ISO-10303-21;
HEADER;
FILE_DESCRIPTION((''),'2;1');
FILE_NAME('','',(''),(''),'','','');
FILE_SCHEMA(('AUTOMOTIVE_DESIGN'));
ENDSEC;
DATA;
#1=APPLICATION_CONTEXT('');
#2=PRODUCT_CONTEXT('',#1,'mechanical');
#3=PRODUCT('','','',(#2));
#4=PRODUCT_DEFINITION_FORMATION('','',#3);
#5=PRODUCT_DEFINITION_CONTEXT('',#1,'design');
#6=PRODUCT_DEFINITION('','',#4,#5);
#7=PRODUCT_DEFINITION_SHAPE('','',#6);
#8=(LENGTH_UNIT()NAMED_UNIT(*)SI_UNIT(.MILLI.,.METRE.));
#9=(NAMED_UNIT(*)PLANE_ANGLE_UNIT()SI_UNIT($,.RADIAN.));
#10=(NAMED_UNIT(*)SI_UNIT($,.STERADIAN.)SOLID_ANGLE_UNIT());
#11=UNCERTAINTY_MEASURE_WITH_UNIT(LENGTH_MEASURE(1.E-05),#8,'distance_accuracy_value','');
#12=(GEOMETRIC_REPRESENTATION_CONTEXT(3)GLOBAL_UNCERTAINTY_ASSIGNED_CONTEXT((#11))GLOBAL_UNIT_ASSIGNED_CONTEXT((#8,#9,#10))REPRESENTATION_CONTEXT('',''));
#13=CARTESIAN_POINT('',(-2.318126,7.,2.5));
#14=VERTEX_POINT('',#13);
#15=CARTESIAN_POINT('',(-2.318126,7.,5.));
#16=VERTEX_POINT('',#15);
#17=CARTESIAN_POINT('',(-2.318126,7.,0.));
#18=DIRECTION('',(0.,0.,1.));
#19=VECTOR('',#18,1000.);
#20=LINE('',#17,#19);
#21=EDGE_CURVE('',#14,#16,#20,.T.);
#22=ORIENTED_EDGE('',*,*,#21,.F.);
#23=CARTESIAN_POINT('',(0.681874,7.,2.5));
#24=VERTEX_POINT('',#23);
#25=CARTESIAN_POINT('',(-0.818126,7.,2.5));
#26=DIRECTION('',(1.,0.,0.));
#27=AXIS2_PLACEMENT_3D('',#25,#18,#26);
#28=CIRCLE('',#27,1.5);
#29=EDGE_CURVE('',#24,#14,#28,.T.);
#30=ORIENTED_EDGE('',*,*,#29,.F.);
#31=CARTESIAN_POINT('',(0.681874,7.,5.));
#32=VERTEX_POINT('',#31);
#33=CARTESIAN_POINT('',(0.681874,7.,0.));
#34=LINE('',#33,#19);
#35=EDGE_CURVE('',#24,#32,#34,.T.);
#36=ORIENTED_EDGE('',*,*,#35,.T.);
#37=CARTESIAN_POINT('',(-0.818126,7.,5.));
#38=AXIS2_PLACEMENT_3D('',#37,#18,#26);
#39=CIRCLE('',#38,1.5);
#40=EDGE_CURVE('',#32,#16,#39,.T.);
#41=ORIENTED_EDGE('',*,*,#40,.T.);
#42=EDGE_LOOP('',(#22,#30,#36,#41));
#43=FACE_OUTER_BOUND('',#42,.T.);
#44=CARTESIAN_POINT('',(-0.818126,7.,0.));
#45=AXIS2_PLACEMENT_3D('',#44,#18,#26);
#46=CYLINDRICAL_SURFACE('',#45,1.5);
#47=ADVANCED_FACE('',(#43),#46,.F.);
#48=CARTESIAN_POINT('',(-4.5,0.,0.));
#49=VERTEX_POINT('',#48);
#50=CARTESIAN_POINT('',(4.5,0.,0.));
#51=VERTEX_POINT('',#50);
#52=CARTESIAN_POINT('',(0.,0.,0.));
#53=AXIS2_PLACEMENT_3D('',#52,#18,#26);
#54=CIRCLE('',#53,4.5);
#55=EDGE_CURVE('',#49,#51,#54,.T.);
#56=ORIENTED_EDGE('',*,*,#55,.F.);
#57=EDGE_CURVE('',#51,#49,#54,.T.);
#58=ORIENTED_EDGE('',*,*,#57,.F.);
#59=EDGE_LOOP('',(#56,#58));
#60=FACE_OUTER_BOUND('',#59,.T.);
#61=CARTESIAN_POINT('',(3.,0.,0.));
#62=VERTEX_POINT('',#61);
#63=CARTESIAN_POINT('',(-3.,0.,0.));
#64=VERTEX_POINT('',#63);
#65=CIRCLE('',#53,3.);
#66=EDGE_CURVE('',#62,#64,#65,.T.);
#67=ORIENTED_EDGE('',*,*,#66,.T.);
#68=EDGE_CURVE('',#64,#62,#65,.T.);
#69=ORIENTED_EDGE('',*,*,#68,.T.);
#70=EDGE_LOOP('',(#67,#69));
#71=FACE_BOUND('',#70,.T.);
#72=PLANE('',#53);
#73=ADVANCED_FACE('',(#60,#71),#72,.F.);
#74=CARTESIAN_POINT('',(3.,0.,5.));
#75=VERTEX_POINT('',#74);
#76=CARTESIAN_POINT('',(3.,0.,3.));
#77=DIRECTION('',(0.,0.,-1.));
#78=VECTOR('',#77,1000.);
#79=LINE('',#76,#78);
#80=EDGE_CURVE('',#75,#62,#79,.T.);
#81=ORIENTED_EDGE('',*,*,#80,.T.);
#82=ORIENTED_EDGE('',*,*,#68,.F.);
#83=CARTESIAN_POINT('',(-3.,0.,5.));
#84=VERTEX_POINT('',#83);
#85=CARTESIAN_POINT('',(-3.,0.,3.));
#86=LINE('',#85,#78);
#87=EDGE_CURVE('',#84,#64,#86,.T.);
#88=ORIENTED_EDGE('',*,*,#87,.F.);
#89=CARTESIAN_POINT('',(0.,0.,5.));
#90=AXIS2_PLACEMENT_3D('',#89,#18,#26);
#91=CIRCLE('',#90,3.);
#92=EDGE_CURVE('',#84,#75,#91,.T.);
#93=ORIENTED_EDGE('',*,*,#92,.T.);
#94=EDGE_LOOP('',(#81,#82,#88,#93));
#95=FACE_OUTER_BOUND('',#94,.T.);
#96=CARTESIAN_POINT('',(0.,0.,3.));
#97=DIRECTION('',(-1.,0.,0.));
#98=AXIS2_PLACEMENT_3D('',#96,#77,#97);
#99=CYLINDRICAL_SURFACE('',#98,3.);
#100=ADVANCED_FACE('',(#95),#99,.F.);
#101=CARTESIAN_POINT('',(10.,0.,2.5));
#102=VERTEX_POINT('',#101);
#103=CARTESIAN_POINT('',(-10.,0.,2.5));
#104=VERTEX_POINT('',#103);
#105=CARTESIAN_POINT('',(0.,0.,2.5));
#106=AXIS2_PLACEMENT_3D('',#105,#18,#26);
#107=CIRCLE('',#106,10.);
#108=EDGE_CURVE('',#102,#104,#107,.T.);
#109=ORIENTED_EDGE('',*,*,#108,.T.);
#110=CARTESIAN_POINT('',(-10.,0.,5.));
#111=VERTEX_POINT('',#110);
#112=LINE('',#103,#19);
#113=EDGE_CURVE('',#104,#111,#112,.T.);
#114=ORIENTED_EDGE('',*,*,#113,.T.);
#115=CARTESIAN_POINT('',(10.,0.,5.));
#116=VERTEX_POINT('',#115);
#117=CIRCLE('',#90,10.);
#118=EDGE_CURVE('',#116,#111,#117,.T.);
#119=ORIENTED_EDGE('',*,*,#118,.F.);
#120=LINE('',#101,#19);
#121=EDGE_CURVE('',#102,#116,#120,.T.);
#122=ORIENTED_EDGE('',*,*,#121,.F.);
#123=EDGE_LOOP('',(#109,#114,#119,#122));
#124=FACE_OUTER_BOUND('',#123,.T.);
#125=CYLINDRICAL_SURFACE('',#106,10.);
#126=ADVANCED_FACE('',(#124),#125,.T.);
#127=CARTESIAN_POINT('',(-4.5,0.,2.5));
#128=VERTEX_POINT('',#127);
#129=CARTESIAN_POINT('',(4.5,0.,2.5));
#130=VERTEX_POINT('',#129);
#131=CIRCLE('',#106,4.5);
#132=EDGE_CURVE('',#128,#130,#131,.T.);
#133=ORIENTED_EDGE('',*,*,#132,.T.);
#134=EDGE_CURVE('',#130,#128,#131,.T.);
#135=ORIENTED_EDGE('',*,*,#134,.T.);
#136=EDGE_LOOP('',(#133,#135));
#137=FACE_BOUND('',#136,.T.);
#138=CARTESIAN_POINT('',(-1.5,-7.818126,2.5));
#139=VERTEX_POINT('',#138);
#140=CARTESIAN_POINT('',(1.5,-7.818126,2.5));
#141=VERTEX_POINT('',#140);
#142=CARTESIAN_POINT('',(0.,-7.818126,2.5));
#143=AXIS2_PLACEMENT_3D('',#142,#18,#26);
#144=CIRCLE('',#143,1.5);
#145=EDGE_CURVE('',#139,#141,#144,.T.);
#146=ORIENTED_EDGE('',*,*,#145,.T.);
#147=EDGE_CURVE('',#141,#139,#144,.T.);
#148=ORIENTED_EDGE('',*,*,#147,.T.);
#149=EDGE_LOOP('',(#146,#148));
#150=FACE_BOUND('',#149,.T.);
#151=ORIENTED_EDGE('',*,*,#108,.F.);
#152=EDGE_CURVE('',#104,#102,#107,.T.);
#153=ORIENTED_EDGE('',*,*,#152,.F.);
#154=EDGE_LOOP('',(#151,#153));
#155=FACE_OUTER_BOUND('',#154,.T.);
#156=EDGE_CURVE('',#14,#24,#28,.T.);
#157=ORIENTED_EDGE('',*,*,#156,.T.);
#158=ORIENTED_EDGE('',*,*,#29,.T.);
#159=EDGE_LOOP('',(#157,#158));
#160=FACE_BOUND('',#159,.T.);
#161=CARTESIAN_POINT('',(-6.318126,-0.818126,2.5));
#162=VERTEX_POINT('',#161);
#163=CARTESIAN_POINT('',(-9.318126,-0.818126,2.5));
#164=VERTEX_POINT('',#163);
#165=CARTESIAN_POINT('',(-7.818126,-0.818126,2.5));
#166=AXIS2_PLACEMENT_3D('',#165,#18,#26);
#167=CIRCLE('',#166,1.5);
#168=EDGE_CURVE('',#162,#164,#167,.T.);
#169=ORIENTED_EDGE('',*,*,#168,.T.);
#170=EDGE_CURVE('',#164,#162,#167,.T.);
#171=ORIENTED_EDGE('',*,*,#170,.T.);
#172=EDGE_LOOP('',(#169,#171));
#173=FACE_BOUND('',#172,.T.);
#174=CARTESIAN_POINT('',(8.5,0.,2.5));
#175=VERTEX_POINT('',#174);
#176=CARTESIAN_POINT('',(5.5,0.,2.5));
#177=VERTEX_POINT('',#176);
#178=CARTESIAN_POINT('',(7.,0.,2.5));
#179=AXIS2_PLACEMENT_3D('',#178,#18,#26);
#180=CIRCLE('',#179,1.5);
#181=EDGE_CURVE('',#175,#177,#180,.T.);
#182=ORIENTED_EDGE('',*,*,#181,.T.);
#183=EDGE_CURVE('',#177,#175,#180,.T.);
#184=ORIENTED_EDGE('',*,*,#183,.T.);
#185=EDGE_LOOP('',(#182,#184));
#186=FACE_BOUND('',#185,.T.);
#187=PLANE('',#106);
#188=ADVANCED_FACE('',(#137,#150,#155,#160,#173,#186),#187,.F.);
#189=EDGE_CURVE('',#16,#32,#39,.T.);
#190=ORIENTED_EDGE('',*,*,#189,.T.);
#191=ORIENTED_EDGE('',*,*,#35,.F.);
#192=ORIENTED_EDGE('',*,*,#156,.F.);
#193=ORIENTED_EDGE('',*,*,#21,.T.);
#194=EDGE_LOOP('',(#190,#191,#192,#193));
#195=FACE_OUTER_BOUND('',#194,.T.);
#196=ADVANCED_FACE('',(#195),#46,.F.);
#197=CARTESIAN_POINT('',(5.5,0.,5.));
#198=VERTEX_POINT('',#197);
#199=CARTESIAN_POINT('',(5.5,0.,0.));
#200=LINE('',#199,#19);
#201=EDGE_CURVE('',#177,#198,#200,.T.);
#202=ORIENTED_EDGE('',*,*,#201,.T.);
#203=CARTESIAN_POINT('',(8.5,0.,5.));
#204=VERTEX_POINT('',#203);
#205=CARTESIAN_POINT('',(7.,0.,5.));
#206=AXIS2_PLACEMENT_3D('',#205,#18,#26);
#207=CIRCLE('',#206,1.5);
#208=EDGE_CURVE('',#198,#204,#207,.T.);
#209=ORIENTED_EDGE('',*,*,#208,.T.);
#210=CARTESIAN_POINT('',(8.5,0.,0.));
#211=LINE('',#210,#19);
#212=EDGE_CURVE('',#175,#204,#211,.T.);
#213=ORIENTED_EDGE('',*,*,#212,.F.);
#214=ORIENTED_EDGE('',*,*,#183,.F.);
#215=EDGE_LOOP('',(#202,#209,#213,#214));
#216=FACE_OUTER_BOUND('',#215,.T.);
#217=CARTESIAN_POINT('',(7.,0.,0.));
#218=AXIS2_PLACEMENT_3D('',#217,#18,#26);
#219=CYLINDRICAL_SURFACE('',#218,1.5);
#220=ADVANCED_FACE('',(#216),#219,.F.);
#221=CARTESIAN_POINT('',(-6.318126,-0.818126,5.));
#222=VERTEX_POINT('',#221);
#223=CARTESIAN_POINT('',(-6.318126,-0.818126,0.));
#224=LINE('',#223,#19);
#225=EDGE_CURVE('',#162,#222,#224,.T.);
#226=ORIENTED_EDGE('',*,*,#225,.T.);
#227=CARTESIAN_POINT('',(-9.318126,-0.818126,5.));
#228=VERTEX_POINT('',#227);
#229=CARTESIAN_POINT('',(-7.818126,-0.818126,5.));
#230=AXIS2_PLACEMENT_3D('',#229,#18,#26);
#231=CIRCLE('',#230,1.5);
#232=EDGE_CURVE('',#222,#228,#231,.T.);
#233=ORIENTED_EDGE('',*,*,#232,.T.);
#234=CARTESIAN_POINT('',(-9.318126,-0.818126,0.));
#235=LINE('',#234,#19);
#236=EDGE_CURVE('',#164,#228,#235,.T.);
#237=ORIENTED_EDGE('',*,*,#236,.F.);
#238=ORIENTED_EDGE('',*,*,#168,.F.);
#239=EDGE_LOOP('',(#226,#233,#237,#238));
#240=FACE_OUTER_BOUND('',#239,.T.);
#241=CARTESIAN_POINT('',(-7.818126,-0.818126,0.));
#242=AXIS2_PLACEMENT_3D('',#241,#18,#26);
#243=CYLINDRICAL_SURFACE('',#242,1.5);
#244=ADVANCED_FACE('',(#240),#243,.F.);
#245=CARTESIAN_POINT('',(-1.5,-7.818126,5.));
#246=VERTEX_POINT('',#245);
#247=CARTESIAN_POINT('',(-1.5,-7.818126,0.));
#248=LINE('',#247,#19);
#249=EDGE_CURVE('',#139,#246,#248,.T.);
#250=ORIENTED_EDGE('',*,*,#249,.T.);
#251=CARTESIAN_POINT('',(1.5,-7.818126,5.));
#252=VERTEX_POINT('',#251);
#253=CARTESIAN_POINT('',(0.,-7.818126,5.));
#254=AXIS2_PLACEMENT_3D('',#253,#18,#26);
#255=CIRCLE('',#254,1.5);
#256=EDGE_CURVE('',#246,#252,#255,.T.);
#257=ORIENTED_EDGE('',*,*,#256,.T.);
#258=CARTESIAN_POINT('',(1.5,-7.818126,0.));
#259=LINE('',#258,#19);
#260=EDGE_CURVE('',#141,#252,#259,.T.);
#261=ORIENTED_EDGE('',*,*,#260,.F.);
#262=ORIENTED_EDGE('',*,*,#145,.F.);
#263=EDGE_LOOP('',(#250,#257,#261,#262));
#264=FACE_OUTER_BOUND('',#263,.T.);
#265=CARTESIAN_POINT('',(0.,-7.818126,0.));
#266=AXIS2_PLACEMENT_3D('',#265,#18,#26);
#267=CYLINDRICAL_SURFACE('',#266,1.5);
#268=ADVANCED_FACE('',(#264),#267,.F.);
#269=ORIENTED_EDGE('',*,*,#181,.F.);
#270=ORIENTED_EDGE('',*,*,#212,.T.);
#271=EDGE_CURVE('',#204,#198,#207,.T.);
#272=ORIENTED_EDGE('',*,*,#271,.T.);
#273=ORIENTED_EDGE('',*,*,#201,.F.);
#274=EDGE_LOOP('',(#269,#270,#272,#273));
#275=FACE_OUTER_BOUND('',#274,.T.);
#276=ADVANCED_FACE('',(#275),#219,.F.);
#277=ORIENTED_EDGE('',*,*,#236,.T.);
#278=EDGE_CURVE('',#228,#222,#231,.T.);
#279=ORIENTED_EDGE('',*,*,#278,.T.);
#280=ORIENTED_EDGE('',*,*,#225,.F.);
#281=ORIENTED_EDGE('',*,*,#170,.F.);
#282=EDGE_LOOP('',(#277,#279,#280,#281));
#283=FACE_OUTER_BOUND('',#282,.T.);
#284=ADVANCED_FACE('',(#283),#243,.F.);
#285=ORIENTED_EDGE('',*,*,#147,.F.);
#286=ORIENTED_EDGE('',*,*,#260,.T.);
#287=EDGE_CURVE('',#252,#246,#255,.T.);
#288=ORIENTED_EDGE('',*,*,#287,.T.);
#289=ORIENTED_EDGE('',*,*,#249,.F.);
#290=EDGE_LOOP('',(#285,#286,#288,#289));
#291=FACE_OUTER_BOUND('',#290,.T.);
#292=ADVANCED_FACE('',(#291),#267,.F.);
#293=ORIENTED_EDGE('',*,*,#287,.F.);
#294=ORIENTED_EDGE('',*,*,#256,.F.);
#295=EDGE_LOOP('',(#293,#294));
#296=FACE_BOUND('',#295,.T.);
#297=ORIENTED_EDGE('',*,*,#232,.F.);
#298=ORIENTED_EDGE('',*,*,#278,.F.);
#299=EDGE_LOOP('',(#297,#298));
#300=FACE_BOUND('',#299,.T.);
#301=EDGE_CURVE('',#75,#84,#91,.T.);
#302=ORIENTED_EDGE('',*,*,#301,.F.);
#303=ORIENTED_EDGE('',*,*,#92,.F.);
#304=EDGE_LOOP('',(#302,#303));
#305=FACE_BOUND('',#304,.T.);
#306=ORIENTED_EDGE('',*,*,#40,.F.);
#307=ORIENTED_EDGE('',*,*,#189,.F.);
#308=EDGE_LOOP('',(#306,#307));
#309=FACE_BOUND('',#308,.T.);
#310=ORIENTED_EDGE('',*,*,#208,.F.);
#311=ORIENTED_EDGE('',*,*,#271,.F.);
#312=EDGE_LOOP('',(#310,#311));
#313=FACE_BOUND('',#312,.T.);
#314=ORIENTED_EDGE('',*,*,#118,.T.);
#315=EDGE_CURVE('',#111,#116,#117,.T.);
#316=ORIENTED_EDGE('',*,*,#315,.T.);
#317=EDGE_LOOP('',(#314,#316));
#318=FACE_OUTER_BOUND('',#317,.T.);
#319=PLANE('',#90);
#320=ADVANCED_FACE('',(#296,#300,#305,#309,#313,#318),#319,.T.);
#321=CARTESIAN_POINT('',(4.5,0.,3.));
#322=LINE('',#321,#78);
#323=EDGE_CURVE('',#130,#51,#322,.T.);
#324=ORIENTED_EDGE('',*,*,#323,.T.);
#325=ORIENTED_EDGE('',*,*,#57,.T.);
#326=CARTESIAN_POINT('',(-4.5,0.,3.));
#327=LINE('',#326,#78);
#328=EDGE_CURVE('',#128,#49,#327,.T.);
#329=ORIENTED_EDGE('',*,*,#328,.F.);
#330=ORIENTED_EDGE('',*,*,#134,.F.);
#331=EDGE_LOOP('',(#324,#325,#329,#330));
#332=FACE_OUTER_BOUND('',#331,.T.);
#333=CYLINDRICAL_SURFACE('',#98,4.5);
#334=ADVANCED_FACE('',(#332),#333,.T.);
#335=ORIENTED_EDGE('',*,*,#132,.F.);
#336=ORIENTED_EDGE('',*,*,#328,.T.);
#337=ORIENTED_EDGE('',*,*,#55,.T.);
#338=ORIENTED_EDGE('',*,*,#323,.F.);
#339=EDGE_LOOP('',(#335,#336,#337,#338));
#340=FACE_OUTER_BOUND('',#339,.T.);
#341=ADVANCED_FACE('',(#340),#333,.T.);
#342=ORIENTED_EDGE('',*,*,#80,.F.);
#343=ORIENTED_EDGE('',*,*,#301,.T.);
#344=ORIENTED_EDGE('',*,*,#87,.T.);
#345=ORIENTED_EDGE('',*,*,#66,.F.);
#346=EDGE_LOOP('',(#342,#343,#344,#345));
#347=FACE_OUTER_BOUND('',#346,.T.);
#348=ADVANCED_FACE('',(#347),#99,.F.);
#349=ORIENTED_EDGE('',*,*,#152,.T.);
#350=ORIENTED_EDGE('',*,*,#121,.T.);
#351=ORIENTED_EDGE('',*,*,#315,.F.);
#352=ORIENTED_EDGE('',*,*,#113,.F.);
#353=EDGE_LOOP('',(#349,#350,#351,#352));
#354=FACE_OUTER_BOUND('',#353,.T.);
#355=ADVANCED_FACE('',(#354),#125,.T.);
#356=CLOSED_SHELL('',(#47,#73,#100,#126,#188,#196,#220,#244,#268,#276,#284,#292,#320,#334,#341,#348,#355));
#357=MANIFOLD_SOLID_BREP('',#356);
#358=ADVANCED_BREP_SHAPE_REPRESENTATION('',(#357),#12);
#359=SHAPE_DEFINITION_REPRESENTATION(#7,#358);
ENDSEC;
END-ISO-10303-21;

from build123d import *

# Parameters (mm, degrees)
SKETCH3_R                = 4.5
SKETCH3_R_2              = 3
BOSS_EXTRUDE1_DEPTH      = 3
BOSS_EXTRUDE2_DEPTH      = 2
BOSS_EXTRUDE2_DEPTH_BACK = 0.5
SKETCH4_R                = 10
SKETCH4_R_2              = 3
SKETCH5_R                = 1.5
CUT_EXTRUDE1_DEPTH       = 16


with BuildPart() as part:
    # Sketch3 → Boss-Extrude1 (new body)
    with BuildSketch(Plane.XY):
        Circle(SKETCH3_R)
        Circle(SKETCH3_R_2, mode=Mode.SUBTRACT)
    extrude(amount=BOSS_EXTRUDE1_DEPTH)

    # Sketch4 → Boss-Extrude2 (add, two sides: drawn at the far end of the back side and taken through both)
    with BuildSketch(Plane.XY.offset(3).offset(-BOSS_EXTRUDE2_DEPTH_BACK)):
        Circle(SKETCH4_R)
        Circle(SKETCH4_R_2, mode=Mode.SUBTRACT)
    extrude(amount=BOSS_EXTRUDE2_DEPTH + BOSS_EXTRUDE2_DEPTH_BACK)

    # Sketch5 → Cut-Extrude1 (cut, through all)
    with BuildSketch(Plane.XY.offset(5)):
        with Locations((7, 0)):
            Circle(SKETCH5_R)
        with Locations((-0.818126129, 7)):
            Circle(SKETCH5_R)
        with Locations((0, -7.818126129)):
            Circle(SKETCH5_R)
        with Locations((-7.818126129, -0.818126129)):
            Circle(SKETCH5_R)
    extrude(amount=-CUT_EXTRUDE1_DEPTH, mode=Mode.SUBTRACT)


solid = part.part
